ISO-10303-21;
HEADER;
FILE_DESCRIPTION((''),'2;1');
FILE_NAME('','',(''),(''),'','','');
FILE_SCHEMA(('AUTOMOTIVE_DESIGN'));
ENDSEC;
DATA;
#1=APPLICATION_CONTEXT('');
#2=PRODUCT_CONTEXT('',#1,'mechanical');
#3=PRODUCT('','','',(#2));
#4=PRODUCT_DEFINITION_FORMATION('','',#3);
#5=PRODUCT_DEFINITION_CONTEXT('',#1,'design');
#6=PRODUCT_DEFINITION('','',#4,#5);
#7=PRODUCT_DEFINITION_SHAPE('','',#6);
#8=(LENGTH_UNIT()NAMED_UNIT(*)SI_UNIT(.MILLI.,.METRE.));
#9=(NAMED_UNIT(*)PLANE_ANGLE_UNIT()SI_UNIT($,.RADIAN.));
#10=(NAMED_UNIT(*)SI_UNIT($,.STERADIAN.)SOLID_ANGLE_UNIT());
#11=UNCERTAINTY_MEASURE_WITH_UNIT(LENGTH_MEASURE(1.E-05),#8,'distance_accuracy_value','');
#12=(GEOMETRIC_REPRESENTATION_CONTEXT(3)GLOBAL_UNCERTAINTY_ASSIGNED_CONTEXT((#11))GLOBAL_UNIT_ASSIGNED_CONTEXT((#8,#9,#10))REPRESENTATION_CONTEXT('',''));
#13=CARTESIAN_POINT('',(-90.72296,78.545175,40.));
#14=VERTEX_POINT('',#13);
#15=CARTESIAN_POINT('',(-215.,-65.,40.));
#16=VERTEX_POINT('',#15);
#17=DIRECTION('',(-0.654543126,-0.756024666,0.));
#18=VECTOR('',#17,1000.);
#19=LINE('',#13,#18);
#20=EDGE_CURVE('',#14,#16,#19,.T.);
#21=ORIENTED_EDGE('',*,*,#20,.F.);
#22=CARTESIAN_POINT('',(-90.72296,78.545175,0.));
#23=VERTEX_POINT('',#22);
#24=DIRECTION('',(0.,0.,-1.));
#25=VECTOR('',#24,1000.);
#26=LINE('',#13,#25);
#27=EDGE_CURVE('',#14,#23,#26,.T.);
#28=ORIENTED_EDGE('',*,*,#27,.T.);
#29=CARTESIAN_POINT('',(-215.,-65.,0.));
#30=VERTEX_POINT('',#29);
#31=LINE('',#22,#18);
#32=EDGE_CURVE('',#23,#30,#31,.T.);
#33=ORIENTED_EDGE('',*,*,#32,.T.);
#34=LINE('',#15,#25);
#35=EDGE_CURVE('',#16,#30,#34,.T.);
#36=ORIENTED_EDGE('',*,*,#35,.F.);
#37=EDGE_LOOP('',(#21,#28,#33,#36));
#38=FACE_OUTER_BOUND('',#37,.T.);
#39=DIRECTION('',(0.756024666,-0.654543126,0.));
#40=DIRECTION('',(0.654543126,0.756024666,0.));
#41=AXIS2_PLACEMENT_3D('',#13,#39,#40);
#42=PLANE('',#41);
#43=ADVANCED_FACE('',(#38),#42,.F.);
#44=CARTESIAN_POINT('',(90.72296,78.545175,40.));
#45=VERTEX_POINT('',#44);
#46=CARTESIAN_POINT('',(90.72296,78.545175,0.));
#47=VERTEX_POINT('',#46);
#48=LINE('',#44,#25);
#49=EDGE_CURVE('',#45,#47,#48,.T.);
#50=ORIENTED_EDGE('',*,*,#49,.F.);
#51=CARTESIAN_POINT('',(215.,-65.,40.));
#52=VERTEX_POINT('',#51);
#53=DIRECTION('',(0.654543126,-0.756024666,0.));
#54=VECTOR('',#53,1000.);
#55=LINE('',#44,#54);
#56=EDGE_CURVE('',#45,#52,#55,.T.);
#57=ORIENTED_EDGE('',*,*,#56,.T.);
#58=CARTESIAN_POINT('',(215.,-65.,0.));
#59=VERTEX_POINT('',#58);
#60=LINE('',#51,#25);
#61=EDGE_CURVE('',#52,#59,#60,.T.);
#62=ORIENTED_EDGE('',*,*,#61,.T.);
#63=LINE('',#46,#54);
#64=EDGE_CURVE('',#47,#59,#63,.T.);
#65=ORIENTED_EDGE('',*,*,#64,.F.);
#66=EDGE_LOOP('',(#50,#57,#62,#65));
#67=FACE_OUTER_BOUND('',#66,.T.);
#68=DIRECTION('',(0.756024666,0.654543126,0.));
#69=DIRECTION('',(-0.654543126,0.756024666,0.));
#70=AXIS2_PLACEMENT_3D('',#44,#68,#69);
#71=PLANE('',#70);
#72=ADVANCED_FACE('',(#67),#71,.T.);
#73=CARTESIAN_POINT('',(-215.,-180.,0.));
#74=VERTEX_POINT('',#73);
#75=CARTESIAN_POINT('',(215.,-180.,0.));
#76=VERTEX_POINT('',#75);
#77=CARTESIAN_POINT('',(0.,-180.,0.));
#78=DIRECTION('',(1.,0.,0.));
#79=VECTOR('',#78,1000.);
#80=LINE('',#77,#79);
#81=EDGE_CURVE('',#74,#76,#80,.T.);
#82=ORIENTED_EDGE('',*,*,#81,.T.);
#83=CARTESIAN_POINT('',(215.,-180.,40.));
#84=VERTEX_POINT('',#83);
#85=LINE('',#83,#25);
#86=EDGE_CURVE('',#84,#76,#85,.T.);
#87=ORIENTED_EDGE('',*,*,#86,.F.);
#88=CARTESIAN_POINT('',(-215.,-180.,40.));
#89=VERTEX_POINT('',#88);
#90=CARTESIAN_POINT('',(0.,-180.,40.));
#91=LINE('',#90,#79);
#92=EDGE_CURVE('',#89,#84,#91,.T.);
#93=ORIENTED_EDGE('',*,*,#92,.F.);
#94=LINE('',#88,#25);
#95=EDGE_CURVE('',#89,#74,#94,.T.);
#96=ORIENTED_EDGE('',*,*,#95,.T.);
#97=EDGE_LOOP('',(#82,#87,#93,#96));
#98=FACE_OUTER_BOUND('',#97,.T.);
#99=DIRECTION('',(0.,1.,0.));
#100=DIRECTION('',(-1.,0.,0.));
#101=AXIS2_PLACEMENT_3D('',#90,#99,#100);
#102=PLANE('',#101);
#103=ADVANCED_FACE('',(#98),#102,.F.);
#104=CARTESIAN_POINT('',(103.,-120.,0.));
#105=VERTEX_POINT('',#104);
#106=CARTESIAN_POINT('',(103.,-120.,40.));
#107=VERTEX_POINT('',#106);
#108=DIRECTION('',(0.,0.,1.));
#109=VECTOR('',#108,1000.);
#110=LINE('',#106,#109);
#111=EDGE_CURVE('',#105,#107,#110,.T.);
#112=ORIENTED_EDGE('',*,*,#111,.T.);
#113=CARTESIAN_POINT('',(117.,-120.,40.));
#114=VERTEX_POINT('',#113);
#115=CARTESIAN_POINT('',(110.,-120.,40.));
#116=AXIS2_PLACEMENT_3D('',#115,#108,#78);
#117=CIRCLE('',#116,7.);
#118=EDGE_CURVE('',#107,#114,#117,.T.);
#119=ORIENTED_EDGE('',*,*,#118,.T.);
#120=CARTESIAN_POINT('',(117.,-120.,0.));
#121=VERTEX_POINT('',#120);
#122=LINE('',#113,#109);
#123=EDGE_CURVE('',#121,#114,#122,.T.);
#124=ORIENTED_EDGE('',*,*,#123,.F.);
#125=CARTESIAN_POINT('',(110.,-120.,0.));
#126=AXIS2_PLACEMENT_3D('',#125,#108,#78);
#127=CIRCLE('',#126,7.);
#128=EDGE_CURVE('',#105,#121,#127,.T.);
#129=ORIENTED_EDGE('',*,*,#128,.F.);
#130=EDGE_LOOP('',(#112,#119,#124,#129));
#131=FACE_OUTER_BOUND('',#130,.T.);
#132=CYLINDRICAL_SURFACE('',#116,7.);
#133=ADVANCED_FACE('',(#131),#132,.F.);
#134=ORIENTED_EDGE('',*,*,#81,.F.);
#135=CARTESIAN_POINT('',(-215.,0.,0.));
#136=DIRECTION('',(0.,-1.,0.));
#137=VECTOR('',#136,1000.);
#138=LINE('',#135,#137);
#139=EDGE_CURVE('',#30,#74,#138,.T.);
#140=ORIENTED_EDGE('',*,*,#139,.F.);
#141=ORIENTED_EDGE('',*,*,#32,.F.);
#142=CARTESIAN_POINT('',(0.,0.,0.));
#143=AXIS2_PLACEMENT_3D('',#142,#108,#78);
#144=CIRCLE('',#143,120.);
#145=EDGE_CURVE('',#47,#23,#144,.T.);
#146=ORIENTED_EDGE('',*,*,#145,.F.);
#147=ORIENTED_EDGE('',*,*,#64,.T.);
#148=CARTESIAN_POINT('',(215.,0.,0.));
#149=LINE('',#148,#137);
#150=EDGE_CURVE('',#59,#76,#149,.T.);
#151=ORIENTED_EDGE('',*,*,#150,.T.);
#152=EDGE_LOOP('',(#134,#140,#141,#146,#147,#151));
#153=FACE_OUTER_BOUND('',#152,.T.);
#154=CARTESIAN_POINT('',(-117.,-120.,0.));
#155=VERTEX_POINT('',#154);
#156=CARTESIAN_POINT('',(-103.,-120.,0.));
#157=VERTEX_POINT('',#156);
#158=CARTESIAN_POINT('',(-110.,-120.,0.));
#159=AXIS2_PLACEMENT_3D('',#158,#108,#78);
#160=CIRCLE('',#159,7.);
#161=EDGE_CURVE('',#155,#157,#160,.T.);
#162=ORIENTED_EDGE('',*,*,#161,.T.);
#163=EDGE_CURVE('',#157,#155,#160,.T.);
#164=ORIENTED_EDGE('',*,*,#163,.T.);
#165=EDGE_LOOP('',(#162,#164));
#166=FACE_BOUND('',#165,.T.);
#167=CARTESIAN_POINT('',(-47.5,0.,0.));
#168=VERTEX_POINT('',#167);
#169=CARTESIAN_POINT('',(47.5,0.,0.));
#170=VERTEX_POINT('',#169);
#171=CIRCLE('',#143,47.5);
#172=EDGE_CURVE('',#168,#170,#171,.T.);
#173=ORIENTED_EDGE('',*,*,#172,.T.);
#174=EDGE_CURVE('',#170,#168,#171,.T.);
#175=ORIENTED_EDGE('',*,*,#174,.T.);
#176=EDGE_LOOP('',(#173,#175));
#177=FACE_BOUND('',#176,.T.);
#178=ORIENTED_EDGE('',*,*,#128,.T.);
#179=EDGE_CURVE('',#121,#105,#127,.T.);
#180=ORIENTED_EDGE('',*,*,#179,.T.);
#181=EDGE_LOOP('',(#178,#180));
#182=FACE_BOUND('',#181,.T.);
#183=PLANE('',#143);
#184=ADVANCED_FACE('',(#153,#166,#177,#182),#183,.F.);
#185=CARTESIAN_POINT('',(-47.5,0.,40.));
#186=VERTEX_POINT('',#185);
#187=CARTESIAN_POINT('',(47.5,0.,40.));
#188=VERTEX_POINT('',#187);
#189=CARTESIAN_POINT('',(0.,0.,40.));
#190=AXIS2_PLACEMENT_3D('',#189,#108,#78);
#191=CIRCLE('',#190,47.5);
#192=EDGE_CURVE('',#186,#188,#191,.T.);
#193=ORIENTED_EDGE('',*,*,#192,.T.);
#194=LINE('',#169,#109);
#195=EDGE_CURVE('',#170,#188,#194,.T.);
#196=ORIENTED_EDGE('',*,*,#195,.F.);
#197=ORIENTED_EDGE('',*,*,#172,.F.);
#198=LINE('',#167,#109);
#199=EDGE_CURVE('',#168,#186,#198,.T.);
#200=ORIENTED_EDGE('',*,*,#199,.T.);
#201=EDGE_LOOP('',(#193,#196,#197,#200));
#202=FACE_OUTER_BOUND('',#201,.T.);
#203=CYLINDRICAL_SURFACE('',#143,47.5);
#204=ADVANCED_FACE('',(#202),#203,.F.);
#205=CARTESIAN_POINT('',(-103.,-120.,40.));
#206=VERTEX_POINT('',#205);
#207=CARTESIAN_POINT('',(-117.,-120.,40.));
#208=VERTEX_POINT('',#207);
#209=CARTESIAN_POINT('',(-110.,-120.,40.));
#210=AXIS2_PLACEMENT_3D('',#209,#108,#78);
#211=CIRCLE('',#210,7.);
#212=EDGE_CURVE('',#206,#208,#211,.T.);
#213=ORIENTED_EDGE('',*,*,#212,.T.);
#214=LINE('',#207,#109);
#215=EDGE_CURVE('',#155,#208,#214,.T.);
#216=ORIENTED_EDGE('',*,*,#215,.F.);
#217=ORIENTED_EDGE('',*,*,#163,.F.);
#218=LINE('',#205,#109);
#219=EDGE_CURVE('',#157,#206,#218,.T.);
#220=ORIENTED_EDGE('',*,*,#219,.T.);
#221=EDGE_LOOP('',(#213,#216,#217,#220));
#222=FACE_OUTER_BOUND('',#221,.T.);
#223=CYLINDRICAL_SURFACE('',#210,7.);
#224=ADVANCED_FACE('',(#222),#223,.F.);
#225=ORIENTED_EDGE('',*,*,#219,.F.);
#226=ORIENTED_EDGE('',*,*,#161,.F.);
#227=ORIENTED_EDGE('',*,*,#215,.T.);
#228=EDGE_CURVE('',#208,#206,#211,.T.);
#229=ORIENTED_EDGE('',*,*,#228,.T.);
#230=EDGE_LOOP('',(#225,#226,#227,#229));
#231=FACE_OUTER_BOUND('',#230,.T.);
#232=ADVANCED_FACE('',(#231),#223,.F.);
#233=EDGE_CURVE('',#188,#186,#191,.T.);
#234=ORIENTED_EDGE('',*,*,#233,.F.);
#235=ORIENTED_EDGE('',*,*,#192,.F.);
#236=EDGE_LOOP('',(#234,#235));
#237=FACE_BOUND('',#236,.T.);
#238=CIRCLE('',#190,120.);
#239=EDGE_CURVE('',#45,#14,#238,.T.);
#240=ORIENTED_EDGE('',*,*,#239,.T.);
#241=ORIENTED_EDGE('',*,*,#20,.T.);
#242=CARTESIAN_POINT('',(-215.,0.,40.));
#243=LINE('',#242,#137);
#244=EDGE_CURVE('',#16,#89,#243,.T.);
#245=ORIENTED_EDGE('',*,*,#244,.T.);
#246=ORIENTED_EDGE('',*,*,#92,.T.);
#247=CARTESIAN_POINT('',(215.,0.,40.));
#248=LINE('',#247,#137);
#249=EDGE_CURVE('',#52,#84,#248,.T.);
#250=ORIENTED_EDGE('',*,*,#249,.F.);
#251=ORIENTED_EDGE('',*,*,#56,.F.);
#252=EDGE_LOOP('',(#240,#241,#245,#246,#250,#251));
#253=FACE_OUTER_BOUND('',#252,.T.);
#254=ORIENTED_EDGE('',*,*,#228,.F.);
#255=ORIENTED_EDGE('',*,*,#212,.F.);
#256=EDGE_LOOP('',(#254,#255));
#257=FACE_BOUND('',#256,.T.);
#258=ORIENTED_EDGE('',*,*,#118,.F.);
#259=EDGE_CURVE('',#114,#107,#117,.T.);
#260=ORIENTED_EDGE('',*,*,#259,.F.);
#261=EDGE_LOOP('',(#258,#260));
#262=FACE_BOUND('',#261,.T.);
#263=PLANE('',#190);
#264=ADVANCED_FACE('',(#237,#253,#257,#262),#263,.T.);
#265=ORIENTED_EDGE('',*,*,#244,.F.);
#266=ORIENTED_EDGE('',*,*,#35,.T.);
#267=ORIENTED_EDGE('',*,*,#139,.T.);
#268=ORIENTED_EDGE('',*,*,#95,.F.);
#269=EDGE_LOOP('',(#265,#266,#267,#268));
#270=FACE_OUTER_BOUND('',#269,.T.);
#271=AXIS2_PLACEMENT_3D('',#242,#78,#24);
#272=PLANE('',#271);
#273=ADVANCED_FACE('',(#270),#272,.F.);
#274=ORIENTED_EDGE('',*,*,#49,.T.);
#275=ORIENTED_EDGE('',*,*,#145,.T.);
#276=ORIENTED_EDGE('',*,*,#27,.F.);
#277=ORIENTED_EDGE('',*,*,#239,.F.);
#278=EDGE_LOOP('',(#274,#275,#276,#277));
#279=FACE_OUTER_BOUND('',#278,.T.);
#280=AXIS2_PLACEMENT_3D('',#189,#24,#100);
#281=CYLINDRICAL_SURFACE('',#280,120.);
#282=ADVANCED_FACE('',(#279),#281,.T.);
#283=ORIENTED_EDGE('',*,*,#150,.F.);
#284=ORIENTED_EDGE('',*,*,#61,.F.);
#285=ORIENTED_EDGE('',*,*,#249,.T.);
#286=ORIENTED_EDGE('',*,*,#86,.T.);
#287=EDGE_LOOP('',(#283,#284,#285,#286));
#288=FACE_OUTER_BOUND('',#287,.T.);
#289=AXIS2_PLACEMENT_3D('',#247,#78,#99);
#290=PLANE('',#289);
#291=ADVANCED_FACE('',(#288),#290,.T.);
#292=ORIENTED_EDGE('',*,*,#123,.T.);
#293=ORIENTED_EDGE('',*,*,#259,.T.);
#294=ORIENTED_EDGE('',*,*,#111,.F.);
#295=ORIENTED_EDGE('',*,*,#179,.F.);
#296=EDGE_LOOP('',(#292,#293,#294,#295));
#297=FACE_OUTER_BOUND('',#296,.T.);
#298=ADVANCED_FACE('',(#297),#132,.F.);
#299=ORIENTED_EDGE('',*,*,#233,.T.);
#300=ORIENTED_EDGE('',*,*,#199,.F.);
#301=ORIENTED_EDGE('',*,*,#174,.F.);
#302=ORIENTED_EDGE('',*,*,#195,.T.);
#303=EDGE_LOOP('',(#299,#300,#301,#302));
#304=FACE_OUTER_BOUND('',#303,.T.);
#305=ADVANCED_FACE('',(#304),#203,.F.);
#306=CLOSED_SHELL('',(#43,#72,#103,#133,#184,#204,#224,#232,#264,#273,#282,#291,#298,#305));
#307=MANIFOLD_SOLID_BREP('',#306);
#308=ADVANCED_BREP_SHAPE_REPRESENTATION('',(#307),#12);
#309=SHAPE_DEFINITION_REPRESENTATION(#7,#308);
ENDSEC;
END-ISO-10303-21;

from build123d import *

# Parameters (mm, degrees)
BOSS_EXTRUDE1_DEPTH = 40
SKETCH2_R           = 47.5
CUT_EXTRUDE1_DEPTH  = 284.240180765
M16_TAPPED_HOLE1_D  = 14


with BuildPart() as part:
    # Sketch1 → Boss-Extrude1 (new body)
    with BuildSketch(Plane.XY):
        with BuildLine():
            Line((-215, -180), (215, -180))
            Line((215, -180), (215, -65))
            Line((215, -65), (90.722959932, 78.545175161))
            ThreePointArc((90.722959932, 78.545175161), (0, 120), (-90.722959932, 78.545175161))
            Line((-90.722959932, 78.545175161), (-215, -65))
            Line((-215, -65), (-215, -180))
        make_face()
    extrude(amount=BOSS_EXTRUDE1_DEPTH)

    # Sketch2 → Cut-Extrude1 (cut, through all)
    with BuildSketch(Plane.XY.offset(40)):
        Circle(SKETCH2_R)
    extrude(amount=-CUT_EXTRUDE1_DEPTH, mode=Mode.SUBTRACT)

    # M16 Tapped Hole1 (through all)
    with Locations(Plane.XY.offset(40)):
        with Locations((-110, -120), (110, -120)):
            Hole(M16_TAPPED_HOLE1_D / 2)


solid = part.part
